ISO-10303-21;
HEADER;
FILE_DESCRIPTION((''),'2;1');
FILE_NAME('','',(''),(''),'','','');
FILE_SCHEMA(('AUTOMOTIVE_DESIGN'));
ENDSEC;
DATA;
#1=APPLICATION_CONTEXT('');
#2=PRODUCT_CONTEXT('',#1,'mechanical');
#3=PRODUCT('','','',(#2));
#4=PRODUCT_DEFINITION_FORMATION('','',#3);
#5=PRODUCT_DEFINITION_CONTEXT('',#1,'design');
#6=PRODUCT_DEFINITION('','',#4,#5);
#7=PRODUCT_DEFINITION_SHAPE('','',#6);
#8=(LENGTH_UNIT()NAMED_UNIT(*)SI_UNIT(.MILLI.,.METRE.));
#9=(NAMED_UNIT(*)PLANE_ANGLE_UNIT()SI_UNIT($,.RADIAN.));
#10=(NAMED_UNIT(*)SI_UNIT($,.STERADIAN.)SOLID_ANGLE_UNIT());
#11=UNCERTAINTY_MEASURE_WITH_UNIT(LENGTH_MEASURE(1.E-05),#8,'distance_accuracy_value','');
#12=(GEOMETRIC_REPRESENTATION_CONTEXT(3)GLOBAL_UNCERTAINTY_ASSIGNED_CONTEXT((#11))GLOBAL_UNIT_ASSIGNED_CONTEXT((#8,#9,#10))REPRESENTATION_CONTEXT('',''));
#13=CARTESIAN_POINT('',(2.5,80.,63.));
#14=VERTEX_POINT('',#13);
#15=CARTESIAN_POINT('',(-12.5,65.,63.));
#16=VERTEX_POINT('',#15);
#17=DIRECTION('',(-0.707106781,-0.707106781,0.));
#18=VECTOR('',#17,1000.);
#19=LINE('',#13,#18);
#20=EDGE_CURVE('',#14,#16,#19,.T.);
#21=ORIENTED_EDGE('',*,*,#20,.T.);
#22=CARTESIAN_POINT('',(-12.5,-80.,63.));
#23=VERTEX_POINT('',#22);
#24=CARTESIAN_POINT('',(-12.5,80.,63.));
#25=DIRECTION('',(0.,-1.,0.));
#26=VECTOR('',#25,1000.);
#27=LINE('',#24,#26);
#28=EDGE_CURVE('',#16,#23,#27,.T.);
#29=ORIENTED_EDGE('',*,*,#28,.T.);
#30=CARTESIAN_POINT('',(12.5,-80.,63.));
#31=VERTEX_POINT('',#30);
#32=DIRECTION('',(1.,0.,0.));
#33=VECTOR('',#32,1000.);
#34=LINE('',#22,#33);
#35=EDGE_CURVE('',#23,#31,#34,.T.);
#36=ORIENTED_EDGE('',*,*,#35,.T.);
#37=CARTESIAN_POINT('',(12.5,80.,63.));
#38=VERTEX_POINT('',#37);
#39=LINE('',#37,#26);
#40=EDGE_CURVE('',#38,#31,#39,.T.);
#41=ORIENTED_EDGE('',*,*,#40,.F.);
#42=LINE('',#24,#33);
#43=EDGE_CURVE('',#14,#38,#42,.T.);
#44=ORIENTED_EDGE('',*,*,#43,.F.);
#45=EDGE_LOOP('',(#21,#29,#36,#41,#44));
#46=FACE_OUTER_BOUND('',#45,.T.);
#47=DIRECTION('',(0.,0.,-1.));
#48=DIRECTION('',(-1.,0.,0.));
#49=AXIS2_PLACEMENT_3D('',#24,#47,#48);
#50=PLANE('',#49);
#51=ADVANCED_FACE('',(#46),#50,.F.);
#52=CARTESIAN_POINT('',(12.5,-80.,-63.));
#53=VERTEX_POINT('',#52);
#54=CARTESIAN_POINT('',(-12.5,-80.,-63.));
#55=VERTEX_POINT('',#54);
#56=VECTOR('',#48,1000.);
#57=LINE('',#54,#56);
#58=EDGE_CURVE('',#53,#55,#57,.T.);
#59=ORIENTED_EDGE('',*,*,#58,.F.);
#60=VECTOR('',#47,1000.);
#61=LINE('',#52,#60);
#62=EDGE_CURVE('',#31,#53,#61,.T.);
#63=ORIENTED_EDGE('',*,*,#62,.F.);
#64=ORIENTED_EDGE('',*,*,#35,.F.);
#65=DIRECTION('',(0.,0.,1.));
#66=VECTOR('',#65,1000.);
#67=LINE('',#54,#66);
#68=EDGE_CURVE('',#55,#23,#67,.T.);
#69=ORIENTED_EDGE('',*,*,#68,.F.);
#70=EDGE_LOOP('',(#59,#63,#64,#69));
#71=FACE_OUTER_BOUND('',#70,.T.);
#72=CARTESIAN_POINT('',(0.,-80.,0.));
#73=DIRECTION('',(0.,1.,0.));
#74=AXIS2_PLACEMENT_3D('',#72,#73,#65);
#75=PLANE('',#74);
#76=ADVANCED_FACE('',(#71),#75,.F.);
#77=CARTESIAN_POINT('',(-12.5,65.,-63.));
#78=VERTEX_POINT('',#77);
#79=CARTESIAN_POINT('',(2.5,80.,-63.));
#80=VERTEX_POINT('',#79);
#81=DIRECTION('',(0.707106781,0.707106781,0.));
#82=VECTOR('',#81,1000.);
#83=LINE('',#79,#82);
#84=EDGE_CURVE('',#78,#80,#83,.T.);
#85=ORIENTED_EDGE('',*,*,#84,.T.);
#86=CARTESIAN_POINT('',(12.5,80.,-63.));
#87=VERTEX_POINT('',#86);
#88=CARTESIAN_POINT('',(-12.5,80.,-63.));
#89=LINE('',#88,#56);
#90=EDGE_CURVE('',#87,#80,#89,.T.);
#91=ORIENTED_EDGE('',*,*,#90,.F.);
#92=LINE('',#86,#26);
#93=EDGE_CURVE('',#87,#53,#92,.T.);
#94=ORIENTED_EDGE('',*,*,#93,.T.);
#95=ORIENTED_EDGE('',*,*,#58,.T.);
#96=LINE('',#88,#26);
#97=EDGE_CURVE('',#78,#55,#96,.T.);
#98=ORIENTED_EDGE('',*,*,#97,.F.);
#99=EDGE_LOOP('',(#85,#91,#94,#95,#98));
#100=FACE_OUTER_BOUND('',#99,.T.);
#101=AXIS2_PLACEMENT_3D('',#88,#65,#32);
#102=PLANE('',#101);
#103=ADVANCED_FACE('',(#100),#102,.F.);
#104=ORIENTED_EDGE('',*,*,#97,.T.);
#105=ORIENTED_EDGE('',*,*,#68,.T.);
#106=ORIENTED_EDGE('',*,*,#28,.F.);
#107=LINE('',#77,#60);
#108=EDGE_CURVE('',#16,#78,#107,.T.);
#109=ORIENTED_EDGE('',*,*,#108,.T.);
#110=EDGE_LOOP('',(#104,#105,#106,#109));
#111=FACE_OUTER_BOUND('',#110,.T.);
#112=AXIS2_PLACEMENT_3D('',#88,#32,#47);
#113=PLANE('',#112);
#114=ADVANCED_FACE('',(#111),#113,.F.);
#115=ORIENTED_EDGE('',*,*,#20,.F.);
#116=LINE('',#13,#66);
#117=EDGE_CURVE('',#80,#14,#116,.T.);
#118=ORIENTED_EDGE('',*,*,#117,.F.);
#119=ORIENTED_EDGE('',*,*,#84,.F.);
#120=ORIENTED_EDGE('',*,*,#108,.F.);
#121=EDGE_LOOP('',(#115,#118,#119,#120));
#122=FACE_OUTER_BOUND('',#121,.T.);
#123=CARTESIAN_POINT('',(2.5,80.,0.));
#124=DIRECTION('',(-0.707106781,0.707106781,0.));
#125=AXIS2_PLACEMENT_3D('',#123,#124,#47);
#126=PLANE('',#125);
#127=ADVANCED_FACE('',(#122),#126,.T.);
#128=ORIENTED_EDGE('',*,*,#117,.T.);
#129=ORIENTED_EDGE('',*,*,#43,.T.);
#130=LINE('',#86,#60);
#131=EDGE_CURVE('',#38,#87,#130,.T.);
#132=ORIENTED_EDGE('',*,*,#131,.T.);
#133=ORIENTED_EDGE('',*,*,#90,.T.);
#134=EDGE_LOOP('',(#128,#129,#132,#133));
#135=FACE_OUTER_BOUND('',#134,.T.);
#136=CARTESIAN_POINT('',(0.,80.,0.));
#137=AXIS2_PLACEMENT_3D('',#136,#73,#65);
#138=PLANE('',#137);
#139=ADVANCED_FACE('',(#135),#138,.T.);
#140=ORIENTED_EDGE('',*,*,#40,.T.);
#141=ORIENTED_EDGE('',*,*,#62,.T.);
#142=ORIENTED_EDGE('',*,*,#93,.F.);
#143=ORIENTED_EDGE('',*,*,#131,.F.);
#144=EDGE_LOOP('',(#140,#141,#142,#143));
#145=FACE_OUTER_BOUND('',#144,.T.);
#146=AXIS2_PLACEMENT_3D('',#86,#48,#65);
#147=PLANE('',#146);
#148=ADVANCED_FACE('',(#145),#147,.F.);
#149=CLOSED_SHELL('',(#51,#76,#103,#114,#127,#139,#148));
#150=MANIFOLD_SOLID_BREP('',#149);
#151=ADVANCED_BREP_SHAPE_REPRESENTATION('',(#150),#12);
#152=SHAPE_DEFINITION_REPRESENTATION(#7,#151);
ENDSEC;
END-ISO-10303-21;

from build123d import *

# Parameters (mm, degrees)
SKETCH2_W           = 25
SKETCH2_H           = 126
BOSS_EXTRUDE1_DEPTH = 80
CHAMFER1_SIZE       = 15


with BuildPart() as part:
    # Sketch2 → Boss-Extrude1 (new, symmetric)
    with BuildSketch(Plane(origin=(0, 0, 0), x_dir=(1, 0, 0), z_dir=(0, 1, 0))):
        Rectangle(SKETCH2_W, SKETCH2_H)
    extrude(amount=BOSS_EXTRUDE1_DEPTH, both=True)

    # Chamfer1
    chamfer1_edges = [part.edges().sort_by_distance(p)[0] for p in [
        (-12.5, 80, 0),
    ]]
    chamfer(chamfer1_edges, length=CHAMFER1_SIZE)


solid = part.part
